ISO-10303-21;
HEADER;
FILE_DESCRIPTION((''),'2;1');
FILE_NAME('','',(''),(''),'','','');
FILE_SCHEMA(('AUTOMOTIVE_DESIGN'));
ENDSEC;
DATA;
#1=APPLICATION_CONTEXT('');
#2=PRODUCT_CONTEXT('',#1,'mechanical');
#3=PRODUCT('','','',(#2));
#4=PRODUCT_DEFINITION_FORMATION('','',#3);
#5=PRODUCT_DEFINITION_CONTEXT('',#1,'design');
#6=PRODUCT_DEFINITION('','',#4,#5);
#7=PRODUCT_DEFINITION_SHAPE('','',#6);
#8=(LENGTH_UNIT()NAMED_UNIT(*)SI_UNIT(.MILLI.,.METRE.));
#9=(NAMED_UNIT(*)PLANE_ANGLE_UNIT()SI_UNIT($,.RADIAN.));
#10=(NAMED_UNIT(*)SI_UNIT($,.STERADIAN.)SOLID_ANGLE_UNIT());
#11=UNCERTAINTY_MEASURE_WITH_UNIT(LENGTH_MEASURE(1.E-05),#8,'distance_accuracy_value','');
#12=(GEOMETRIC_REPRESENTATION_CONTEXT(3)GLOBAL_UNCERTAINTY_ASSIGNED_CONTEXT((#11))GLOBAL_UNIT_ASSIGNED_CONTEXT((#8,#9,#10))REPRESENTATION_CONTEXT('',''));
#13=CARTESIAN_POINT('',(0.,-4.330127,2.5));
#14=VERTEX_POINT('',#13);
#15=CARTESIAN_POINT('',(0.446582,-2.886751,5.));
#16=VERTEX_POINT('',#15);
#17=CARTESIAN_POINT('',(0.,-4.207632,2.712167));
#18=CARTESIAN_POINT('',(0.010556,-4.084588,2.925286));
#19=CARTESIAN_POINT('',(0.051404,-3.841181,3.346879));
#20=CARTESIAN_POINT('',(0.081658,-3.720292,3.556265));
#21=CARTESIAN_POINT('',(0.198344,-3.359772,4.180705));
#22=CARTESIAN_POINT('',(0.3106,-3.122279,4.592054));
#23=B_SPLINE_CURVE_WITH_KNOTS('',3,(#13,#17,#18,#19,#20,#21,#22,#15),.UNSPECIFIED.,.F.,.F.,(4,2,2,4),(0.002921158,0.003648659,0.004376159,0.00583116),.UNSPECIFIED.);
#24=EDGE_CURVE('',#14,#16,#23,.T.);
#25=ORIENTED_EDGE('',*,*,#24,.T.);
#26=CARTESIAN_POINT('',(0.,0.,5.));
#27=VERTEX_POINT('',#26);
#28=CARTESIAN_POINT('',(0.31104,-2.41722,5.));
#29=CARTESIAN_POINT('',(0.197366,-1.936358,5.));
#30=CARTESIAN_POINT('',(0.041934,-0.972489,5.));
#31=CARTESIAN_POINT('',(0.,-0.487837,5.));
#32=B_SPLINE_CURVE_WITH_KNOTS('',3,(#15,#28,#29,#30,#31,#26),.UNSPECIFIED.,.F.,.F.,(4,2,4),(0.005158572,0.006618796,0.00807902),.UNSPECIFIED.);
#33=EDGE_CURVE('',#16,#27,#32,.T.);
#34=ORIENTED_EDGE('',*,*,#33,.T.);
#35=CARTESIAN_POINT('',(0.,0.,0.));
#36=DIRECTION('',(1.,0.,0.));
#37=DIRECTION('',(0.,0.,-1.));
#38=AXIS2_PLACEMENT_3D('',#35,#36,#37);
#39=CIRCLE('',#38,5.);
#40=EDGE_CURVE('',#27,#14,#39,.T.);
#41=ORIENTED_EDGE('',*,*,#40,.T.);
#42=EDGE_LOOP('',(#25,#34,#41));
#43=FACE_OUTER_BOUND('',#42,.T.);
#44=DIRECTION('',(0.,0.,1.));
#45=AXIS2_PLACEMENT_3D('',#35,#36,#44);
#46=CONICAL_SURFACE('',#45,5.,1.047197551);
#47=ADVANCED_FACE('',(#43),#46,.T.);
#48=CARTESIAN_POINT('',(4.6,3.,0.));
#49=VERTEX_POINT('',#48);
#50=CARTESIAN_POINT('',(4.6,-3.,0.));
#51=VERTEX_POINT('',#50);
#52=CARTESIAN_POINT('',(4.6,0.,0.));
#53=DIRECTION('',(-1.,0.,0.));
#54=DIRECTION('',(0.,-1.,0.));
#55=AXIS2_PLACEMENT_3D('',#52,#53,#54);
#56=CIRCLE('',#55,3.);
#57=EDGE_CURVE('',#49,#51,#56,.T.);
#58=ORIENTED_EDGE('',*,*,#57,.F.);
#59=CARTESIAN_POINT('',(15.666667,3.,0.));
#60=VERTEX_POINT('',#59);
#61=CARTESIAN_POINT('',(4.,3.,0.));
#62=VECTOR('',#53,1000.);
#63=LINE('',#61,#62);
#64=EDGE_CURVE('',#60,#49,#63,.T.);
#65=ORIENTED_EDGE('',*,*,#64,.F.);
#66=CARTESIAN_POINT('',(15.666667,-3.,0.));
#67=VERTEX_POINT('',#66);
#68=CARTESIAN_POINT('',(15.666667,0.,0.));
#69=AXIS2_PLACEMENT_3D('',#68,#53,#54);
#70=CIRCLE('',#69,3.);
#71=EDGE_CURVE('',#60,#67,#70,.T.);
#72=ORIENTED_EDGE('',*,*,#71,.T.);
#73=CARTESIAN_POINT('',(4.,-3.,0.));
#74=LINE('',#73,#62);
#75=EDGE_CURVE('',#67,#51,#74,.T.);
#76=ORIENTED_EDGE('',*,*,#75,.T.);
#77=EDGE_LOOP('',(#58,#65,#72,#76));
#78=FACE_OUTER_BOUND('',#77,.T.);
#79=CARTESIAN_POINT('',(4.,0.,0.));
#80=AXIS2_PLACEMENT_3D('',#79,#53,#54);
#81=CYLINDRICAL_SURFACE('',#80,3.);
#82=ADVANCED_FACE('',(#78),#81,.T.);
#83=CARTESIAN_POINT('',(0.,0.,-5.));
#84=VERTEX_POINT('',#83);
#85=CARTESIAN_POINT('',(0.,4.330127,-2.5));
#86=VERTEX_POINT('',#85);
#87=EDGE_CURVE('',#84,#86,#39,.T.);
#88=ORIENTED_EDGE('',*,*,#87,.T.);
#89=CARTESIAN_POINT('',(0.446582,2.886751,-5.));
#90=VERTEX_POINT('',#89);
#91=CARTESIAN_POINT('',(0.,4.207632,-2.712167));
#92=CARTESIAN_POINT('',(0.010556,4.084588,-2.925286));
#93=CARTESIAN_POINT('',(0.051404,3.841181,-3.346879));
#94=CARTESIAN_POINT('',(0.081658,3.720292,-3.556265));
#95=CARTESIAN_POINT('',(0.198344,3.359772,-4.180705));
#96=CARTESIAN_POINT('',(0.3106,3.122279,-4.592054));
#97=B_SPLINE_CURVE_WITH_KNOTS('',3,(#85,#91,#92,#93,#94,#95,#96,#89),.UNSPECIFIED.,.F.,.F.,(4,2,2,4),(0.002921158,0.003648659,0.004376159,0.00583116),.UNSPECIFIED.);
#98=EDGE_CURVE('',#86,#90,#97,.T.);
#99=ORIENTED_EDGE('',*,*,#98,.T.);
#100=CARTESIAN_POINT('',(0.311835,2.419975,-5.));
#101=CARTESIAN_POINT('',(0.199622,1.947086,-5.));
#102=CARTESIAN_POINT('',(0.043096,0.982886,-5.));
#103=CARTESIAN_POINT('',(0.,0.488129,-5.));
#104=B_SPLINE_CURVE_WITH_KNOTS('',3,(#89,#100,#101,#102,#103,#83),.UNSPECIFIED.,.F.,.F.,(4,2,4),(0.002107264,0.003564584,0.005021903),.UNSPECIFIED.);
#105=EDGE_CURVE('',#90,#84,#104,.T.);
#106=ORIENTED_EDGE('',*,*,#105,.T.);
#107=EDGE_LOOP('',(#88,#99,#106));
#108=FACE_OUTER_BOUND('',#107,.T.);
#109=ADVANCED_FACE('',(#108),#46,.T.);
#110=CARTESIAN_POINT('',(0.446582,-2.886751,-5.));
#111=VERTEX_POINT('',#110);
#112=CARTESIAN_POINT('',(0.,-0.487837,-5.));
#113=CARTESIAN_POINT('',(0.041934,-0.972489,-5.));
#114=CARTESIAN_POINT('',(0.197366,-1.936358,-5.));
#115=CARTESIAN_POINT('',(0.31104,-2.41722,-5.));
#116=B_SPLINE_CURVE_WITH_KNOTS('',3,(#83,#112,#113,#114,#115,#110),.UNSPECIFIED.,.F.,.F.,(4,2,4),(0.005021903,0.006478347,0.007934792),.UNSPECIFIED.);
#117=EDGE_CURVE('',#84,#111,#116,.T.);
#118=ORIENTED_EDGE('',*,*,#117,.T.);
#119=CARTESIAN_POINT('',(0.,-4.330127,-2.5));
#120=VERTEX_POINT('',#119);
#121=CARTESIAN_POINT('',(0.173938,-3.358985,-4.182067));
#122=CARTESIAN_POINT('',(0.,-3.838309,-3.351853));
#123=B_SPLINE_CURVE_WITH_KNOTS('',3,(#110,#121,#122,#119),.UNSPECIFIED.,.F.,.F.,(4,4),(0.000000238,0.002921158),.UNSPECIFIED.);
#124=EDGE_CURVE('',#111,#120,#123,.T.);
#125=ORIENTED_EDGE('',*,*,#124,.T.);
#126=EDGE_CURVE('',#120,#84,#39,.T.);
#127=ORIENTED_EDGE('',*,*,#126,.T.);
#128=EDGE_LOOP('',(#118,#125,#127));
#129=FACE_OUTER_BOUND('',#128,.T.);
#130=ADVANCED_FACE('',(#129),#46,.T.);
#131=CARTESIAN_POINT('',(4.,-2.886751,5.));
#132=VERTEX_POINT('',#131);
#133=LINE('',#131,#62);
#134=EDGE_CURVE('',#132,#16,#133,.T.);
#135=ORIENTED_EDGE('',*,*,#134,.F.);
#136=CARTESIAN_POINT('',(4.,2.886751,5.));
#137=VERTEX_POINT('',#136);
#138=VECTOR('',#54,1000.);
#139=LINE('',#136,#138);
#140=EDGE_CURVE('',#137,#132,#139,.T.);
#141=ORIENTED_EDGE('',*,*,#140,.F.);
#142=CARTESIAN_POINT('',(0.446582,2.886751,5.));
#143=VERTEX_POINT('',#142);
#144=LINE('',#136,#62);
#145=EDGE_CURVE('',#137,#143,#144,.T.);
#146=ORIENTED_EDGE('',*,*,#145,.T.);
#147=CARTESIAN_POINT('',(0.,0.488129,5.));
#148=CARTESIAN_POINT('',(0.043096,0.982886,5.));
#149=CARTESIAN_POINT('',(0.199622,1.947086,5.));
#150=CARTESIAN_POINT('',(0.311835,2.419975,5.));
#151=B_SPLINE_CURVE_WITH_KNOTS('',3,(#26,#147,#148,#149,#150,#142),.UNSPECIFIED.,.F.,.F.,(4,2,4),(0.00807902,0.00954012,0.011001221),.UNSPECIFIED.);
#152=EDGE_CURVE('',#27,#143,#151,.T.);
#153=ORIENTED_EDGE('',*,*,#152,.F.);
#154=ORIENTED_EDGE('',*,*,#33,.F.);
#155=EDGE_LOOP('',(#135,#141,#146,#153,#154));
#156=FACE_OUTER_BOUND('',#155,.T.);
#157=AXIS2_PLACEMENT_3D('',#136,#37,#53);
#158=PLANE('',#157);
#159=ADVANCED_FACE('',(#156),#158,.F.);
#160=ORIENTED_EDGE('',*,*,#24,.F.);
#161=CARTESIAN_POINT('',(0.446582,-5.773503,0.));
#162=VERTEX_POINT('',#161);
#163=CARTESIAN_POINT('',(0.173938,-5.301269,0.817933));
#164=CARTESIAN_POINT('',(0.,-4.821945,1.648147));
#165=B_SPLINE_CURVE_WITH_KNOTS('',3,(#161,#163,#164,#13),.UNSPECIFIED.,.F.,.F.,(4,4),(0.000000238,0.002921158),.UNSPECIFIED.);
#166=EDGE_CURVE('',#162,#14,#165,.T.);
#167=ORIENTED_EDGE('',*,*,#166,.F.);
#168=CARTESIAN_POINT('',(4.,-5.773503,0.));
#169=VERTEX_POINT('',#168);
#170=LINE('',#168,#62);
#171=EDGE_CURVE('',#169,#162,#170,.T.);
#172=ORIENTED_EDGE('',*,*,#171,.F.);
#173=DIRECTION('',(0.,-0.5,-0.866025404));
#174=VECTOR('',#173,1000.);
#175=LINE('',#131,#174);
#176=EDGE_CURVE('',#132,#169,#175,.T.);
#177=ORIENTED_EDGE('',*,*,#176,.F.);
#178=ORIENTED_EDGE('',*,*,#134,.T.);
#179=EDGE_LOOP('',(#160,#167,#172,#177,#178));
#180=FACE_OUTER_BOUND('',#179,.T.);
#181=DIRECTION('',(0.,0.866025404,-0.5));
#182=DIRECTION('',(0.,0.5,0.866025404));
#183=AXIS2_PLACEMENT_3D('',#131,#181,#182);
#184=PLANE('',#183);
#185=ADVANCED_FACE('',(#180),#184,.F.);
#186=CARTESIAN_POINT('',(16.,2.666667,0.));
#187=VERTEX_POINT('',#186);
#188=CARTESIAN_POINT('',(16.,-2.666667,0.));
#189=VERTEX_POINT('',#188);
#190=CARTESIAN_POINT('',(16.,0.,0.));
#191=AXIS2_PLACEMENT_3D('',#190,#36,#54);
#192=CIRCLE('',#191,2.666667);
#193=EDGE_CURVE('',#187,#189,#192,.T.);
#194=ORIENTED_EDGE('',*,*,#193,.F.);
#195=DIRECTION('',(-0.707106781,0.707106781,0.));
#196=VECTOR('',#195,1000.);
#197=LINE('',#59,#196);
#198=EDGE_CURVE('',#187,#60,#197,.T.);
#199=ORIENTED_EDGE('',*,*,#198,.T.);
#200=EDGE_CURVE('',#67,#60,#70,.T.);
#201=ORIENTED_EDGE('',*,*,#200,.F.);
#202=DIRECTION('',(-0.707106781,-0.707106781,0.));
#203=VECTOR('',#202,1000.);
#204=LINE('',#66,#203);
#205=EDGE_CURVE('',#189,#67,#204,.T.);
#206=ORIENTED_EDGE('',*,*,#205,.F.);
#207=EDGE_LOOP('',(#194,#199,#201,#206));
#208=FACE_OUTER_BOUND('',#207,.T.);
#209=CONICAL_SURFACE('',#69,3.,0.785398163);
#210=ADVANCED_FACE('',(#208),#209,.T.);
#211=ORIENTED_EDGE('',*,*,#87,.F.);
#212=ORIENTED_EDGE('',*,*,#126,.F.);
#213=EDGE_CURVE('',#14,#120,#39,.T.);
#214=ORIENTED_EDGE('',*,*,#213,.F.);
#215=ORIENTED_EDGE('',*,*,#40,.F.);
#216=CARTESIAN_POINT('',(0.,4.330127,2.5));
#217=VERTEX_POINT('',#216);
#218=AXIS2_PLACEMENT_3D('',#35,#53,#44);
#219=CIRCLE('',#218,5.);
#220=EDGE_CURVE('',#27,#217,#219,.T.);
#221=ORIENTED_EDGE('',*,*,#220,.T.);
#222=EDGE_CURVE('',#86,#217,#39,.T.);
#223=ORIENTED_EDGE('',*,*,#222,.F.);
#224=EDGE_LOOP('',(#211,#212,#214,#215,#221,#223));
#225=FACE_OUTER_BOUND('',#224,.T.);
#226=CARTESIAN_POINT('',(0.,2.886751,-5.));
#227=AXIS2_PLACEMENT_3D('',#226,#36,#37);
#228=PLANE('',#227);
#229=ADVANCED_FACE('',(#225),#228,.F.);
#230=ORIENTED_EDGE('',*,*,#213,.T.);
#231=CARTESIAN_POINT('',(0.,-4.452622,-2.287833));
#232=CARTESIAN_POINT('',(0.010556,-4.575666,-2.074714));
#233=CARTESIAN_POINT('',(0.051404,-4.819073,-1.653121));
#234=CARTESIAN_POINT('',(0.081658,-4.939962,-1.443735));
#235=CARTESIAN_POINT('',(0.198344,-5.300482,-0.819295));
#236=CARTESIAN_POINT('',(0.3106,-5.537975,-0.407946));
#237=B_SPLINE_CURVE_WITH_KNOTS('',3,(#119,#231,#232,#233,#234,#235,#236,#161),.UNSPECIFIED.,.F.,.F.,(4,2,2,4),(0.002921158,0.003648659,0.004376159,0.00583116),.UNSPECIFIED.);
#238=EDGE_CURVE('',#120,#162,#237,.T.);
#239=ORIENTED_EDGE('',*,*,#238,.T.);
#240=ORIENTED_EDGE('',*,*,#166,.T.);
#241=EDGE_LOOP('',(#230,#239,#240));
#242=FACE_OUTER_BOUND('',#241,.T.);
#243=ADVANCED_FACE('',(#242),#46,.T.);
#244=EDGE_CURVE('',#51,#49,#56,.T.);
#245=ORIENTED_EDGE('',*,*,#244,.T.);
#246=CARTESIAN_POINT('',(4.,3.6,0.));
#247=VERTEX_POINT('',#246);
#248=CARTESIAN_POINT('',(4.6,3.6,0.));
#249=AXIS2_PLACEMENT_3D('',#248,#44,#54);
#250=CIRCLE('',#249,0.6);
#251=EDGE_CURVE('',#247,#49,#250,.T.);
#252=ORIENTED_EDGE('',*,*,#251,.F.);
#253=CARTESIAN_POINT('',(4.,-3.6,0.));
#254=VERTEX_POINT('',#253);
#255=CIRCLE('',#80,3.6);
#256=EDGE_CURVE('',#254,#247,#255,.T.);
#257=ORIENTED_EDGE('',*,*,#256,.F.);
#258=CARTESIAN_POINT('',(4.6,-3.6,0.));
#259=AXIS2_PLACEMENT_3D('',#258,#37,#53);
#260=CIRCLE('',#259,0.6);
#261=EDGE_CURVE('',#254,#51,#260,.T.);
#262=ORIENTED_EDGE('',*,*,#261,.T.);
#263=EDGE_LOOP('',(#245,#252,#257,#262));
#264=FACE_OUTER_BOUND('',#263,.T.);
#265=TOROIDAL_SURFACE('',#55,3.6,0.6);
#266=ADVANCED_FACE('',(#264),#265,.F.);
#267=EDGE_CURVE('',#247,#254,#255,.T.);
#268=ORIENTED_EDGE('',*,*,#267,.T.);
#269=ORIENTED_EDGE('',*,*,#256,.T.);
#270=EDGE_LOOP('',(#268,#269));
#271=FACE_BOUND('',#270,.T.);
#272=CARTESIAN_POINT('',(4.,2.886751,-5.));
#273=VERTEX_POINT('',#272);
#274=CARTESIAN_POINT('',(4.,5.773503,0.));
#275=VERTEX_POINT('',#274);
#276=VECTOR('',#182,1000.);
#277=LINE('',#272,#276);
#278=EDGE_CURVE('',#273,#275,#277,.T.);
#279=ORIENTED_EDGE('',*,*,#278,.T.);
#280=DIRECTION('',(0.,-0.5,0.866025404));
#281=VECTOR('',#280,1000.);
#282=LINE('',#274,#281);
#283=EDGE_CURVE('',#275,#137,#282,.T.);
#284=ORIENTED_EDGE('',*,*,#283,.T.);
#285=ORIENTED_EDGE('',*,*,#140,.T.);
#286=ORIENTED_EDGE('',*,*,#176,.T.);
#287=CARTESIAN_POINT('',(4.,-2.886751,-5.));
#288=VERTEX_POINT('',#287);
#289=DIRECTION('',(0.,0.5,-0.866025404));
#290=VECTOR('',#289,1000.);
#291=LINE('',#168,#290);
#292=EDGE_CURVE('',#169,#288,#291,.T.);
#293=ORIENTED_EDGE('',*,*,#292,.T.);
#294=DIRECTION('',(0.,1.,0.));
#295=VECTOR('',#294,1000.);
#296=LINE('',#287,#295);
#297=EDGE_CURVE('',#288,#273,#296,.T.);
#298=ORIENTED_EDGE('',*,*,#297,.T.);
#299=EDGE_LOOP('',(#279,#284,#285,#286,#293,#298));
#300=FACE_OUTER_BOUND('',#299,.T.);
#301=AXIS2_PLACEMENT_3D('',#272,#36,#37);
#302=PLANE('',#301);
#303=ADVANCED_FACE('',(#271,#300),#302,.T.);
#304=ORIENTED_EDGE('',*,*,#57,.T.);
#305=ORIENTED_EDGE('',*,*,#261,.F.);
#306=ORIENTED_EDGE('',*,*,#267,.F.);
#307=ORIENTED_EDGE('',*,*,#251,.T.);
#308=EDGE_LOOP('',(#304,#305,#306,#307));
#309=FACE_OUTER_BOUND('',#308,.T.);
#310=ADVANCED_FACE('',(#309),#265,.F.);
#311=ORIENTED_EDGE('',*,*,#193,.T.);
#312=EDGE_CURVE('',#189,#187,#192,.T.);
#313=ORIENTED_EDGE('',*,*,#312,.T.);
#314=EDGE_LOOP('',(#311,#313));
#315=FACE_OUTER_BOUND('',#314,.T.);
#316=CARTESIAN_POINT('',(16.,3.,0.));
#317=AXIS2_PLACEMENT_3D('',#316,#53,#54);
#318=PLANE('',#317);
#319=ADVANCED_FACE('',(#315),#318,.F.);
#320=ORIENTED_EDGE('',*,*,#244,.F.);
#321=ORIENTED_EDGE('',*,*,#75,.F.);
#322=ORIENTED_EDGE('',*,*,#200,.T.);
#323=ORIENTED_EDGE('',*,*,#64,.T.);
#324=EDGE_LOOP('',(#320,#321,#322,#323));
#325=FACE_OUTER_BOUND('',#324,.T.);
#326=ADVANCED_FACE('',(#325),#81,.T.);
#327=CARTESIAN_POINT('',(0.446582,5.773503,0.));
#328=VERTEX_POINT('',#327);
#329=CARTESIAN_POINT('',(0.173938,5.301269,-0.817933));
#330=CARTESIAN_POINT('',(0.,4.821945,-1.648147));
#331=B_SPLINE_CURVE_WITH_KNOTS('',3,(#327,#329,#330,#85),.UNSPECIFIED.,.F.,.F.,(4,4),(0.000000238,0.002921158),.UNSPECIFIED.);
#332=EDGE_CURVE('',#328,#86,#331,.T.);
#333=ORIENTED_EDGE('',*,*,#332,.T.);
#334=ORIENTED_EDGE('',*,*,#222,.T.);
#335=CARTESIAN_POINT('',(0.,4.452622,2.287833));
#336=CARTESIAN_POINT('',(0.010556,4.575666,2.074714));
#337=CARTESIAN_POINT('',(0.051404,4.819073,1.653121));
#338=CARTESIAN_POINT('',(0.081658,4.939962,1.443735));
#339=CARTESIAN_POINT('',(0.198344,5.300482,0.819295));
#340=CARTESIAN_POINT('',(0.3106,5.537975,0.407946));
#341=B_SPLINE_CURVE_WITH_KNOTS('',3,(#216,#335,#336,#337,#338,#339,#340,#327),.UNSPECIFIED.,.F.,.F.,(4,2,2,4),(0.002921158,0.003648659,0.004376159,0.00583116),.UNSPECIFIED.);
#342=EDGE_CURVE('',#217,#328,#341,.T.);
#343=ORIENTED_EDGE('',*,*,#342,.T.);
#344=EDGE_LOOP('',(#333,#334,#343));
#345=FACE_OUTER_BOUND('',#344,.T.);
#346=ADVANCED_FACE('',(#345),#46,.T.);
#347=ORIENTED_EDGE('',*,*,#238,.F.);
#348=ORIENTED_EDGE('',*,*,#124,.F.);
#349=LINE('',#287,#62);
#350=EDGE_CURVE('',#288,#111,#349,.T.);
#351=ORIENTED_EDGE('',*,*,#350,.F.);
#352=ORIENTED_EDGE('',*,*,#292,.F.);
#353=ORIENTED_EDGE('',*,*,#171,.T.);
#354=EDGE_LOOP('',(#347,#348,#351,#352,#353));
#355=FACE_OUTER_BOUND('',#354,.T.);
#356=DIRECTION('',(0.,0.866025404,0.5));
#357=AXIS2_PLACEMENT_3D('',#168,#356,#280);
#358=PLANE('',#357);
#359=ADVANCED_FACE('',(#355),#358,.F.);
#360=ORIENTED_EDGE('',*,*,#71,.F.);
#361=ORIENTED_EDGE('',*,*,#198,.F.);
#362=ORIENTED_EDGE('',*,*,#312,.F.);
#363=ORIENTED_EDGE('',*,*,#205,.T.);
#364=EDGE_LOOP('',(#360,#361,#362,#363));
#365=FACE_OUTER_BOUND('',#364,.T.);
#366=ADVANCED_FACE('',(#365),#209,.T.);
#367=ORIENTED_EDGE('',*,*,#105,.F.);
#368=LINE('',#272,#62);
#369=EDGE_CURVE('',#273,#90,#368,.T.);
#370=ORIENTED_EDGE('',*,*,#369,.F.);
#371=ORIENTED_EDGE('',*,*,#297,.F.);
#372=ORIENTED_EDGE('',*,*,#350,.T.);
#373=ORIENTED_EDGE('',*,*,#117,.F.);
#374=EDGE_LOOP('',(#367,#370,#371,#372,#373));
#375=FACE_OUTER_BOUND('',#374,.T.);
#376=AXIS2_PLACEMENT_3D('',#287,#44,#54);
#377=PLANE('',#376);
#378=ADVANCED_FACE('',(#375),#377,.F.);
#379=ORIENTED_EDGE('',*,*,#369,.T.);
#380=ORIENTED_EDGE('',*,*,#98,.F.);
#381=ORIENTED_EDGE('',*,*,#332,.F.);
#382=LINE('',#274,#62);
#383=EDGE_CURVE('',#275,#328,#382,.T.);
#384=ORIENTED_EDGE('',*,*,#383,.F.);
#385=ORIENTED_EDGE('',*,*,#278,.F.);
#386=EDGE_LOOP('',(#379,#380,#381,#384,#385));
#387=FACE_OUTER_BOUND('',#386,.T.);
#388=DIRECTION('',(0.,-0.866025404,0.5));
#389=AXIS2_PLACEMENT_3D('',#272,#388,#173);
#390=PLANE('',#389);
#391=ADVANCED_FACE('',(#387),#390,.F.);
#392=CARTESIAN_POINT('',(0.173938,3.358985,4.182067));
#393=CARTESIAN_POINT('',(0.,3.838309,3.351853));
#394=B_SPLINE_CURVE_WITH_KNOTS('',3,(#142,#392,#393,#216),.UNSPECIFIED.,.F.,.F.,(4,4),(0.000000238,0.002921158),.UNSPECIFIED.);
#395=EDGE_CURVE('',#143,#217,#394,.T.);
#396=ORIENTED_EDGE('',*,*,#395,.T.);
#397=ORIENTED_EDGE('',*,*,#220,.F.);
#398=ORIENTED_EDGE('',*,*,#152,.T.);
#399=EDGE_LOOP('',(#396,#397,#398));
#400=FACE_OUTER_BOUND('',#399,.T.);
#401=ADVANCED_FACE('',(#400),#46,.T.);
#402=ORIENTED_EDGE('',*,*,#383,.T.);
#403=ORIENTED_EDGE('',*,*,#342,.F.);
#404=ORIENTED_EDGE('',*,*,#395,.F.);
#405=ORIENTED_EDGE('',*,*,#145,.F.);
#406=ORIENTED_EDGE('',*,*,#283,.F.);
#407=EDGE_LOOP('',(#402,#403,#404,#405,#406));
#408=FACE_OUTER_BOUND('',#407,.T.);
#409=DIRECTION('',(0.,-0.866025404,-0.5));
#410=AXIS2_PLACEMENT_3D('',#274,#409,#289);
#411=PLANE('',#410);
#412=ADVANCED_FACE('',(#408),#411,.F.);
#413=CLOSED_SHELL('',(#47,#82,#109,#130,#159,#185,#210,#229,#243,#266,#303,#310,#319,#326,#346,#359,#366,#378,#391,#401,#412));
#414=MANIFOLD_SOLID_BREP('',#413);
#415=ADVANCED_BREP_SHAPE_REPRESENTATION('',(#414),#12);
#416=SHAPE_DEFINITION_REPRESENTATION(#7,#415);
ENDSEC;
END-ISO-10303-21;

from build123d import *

# Parameters (mm, degrees)
EXTRUDE_1_DEPTH     = 4
SKETCH_4_R          = 10.89
SKETCH_4_R_2        = 5
CUT_EXTRUDE_1_DEPTH = 0.5
CUT_EXTRUDE_1_DRAFT = -60
CHAMFER_2_SIZE      = 0.333333333


with BuildPart() as part:
    # 草图3 → 凸台-拉伸1 (new body)
    with BuildSketch(Plane(origin=(0, 0, 0), x_dir=(0, 0, -1), z_dir=(1, 0, 0))):
        Polygon((5, 2.886751346), (0, 5.773502692), (-5, 2.886751346), (-5, -2.886751346), (0, -5.773502692), (5, -2.886751346), align=None)
    extrude(amount=EXTRUDE_1_DEPTH)


with BuildPart() as cut_extrude_1_tool:
    # 草图4 → 切除-拉伸1 (with draft: the straight prism first)
    with BuildSketch(Plane.ZY):
        Circle(SKETCH_4_R)
        Circle(SKETCH_4_R_2, mode=Mode.SUBTRACT)
    extrude(amount=-CUT_EXTRUDE_1_DEPTH)
    # 切除-拉伸1: the draft: its side faces are tilted about the plane it starts from
    cut_extrude_1_sides = [cut_extrude_1_tool.faces().sort_by_distance(p)[0] for p in [
        (0.25, 0, -10.89),
        (0.25, 0, -5),
    ]]
    draft(cut_extrude_1_sides, Plane.ZY, CUT_EXTRUDE_1_DRAFT)


with BuildPart() as part_1:
    add(part.part)

    # 切除-拉伸1: cut by cut_extrude_1_tool
    add(cut_extrude_1_tool.part, mode=Mode.SUBTRACT)

    # 草图5 → 旋转1 (revolve)
    with BuildSketch(Plane.XY, mode=Mode.PRIVATE) as revolve_1_sk:
        with BuildLine():
            Line((4.6, 3), (16, 3))
            Line((16, 3), (16, 0))
            Line((16, 0), (4, 0))
            Line((4, 0), (4, 3.6))
            ThreePointArc((4, 3.6), (4.175735931, 3.175735931), (4.6, 3))
        make_face()
    revolve(revolve_1_sk.sketch.rotate(Axis((4, 0, 0), (1, 0, 0)), 180), axis=Axis((4, 0, 0), (1, 0, 0)))

    # 倒角2
    chamfer_2_edges = [part_1.edges().sort_by_distance(p)[0] for p in [
        (16, 3, 0),
    ]]
    chamfer(chamfer_2_edges, length=CHAMFER_2_SIZE)


solid = part_1.part
